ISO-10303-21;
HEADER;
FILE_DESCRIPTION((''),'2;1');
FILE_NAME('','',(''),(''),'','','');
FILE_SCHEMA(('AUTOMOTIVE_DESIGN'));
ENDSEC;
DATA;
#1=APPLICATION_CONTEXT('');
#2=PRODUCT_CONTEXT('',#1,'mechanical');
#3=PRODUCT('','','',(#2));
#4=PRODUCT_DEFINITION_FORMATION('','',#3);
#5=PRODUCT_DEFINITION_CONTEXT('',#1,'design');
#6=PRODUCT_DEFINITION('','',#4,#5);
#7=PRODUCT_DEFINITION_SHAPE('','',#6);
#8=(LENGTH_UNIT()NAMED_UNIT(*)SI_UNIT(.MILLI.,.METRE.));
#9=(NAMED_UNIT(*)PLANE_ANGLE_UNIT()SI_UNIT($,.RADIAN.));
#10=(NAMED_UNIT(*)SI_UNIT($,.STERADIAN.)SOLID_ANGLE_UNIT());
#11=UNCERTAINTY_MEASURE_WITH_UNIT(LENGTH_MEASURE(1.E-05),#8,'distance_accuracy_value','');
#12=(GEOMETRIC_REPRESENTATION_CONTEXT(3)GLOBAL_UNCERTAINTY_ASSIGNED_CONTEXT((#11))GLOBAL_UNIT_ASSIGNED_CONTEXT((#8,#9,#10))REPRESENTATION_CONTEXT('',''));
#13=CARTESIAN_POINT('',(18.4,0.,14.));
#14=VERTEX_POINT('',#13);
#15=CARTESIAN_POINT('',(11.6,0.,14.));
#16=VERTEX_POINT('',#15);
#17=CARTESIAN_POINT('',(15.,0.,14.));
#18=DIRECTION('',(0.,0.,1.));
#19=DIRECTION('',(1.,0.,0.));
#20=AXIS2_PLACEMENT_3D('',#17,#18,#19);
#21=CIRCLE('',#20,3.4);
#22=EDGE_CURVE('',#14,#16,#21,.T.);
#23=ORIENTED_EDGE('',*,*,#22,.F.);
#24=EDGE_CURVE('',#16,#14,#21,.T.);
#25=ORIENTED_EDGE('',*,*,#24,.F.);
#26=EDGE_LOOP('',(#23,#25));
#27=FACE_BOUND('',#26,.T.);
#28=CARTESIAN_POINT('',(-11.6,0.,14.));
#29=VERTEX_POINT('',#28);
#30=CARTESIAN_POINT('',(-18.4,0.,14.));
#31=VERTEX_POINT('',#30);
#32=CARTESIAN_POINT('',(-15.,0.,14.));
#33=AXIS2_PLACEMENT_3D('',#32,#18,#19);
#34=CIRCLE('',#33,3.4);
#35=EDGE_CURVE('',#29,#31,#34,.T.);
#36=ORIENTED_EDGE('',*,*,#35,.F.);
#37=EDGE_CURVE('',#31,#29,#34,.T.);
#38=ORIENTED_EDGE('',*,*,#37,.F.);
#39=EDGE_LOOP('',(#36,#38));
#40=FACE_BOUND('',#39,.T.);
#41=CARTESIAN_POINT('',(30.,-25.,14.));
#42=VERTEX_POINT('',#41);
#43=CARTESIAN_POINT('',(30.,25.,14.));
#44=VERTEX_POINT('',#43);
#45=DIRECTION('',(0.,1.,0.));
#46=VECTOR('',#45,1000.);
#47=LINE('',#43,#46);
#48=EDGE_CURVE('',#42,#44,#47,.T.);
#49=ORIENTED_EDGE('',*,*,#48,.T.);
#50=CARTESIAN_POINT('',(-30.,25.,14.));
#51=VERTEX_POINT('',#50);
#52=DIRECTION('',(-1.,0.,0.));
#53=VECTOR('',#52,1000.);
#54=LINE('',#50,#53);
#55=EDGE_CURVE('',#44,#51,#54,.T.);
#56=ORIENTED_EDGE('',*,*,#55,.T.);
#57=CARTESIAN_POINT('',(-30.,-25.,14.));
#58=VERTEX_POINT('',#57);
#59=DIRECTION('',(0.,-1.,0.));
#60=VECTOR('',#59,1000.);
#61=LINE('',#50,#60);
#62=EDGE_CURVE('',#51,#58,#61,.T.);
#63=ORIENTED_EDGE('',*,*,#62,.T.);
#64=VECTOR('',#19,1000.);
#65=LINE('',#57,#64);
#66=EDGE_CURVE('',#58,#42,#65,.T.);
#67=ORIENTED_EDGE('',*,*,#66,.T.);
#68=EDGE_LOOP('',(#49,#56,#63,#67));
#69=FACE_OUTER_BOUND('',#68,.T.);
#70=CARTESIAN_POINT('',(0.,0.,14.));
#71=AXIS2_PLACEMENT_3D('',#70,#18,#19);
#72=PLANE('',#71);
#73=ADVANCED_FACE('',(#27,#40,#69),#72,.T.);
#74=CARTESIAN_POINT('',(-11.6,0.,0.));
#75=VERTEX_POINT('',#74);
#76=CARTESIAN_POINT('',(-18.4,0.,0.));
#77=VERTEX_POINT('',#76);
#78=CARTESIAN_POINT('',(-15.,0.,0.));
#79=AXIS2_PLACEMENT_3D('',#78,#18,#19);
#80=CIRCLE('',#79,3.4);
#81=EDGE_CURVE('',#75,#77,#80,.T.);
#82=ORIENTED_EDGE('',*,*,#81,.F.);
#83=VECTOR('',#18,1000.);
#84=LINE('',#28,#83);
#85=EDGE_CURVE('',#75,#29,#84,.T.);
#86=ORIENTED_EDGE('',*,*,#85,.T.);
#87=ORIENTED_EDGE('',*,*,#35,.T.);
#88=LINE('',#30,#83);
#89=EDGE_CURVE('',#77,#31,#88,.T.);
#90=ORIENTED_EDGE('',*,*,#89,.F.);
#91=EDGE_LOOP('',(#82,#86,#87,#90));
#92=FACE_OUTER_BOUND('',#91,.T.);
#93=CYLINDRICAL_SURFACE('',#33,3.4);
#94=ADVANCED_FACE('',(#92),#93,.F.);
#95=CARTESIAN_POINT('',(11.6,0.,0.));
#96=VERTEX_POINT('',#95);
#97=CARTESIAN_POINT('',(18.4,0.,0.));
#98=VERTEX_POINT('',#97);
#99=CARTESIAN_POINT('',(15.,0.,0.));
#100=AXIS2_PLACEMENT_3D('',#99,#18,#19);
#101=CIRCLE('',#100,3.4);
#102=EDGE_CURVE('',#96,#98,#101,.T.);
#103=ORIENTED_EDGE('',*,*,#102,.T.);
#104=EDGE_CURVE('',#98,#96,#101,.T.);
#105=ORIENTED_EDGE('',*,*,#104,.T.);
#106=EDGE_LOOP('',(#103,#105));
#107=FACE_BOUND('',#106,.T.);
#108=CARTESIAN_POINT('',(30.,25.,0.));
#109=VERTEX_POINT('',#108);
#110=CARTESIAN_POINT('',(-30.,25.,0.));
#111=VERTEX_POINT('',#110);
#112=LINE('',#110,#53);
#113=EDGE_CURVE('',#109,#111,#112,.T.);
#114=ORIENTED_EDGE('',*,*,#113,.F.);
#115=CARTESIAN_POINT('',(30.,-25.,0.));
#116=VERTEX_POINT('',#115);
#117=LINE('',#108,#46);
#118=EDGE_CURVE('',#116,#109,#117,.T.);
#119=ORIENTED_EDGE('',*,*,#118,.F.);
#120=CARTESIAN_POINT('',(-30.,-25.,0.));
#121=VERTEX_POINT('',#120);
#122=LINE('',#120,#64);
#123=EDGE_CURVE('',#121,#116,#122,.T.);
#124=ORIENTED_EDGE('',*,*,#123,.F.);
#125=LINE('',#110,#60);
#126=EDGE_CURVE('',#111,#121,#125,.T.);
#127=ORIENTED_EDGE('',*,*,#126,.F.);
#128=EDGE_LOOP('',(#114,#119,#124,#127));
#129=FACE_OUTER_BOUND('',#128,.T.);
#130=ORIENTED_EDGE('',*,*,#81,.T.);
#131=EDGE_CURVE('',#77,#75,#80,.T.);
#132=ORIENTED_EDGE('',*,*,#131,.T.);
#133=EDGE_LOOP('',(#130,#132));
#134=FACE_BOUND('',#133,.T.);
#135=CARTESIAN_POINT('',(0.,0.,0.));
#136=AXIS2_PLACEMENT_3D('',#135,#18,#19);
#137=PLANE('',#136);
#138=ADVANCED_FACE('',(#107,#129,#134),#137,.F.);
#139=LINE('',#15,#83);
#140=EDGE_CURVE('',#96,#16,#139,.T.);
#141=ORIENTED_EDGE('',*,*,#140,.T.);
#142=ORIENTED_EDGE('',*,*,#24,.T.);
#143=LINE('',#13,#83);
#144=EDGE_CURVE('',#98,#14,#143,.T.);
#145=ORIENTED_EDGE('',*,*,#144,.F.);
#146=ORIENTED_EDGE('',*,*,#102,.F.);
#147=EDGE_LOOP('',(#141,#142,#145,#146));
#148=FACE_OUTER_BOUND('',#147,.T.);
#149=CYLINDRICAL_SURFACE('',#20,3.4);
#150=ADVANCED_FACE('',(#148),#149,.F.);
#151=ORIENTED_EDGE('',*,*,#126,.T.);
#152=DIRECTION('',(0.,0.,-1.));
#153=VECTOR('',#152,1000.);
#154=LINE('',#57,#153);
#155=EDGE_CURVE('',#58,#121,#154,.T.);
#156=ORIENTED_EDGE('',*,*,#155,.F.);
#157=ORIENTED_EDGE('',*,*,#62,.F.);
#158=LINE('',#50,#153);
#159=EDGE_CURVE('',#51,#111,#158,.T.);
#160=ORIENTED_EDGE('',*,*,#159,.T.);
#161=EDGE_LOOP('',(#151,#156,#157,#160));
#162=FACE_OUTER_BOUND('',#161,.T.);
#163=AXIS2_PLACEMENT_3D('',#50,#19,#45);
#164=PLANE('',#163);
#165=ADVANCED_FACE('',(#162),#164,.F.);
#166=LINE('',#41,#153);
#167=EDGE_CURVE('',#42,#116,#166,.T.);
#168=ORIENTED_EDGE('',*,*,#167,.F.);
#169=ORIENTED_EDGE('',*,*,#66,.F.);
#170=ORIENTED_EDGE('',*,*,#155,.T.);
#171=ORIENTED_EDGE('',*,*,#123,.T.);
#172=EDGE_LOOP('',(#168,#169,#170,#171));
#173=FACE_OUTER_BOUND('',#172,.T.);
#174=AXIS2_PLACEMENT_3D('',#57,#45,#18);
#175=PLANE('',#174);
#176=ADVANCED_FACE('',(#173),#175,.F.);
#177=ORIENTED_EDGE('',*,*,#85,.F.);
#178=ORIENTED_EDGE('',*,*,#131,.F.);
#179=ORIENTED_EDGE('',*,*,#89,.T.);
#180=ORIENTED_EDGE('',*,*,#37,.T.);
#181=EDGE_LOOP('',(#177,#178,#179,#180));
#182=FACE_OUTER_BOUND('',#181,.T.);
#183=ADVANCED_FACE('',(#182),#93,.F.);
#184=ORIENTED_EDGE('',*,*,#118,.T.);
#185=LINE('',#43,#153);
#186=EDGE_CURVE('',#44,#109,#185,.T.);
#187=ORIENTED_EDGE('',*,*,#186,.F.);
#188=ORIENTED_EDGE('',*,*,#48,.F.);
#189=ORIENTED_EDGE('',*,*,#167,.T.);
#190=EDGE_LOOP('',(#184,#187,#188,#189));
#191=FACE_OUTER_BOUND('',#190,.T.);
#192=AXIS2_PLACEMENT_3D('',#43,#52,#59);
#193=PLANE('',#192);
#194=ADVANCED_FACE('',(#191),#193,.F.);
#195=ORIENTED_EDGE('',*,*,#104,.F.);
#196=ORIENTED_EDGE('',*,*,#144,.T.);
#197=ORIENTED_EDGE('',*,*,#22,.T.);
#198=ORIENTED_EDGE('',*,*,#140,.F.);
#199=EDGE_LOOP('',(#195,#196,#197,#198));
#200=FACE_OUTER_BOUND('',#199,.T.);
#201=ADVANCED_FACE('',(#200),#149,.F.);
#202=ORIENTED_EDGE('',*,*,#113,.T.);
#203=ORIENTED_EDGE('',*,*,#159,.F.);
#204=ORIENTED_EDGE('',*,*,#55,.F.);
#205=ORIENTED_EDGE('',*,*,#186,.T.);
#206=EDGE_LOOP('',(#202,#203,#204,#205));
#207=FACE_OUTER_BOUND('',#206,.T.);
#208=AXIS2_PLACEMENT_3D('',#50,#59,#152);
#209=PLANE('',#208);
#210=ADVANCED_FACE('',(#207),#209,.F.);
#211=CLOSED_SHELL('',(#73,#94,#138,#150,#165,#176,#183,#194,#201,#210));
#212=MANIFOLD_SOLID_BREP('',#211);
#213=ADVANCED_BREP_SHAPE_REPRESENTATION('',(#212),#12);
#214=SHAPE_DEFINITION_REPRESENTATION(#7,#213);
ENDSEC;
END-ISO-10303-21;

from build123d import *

# Parameters (mm, degrees)
SKETCH1_W             = 60
SKETCH1_H             = 50
BOSS_EXTRUDE1_DEPTH   = 14
M8_TAPPED_HOLE1_D     = 6.8
M8_TAPPED_HOLE1_DEPTH = 19.75
M8_TAPPED_HOLE1_TIP   = 2.042926105


with BuildPart() as part:
    # Sketch1 → Boss-Extrude1 (new body)
    with BuildSketch(Plane.XY):
        Rectangle(SKETCH1_W, SKETCH1_H)
    extrude(amount=BOSS_EXTRUDE1_DEPTH)

    # M8 Tapped Hole1
    with Locations(Plane.XY.offset(14)):
        with Locations((-15, 0), (15, 0)):
            Hole(M8_TAPPED_HOLE1_D / 2, depth=M8_TAPPED_HOLE1_DEPTH)
            with Locations((0, 0, -(M8_TAPPED_HOLE1_DEPTH + M8_TAPPED_HOLE1_TIP / 2))):  # 118° drill point
                Cone(0, M8_TAPPED_HOLE1_D / 2, M8_TAPPED_HOLE1_TIP, mode=Mode.SUBTRACT)


solid = part.part
